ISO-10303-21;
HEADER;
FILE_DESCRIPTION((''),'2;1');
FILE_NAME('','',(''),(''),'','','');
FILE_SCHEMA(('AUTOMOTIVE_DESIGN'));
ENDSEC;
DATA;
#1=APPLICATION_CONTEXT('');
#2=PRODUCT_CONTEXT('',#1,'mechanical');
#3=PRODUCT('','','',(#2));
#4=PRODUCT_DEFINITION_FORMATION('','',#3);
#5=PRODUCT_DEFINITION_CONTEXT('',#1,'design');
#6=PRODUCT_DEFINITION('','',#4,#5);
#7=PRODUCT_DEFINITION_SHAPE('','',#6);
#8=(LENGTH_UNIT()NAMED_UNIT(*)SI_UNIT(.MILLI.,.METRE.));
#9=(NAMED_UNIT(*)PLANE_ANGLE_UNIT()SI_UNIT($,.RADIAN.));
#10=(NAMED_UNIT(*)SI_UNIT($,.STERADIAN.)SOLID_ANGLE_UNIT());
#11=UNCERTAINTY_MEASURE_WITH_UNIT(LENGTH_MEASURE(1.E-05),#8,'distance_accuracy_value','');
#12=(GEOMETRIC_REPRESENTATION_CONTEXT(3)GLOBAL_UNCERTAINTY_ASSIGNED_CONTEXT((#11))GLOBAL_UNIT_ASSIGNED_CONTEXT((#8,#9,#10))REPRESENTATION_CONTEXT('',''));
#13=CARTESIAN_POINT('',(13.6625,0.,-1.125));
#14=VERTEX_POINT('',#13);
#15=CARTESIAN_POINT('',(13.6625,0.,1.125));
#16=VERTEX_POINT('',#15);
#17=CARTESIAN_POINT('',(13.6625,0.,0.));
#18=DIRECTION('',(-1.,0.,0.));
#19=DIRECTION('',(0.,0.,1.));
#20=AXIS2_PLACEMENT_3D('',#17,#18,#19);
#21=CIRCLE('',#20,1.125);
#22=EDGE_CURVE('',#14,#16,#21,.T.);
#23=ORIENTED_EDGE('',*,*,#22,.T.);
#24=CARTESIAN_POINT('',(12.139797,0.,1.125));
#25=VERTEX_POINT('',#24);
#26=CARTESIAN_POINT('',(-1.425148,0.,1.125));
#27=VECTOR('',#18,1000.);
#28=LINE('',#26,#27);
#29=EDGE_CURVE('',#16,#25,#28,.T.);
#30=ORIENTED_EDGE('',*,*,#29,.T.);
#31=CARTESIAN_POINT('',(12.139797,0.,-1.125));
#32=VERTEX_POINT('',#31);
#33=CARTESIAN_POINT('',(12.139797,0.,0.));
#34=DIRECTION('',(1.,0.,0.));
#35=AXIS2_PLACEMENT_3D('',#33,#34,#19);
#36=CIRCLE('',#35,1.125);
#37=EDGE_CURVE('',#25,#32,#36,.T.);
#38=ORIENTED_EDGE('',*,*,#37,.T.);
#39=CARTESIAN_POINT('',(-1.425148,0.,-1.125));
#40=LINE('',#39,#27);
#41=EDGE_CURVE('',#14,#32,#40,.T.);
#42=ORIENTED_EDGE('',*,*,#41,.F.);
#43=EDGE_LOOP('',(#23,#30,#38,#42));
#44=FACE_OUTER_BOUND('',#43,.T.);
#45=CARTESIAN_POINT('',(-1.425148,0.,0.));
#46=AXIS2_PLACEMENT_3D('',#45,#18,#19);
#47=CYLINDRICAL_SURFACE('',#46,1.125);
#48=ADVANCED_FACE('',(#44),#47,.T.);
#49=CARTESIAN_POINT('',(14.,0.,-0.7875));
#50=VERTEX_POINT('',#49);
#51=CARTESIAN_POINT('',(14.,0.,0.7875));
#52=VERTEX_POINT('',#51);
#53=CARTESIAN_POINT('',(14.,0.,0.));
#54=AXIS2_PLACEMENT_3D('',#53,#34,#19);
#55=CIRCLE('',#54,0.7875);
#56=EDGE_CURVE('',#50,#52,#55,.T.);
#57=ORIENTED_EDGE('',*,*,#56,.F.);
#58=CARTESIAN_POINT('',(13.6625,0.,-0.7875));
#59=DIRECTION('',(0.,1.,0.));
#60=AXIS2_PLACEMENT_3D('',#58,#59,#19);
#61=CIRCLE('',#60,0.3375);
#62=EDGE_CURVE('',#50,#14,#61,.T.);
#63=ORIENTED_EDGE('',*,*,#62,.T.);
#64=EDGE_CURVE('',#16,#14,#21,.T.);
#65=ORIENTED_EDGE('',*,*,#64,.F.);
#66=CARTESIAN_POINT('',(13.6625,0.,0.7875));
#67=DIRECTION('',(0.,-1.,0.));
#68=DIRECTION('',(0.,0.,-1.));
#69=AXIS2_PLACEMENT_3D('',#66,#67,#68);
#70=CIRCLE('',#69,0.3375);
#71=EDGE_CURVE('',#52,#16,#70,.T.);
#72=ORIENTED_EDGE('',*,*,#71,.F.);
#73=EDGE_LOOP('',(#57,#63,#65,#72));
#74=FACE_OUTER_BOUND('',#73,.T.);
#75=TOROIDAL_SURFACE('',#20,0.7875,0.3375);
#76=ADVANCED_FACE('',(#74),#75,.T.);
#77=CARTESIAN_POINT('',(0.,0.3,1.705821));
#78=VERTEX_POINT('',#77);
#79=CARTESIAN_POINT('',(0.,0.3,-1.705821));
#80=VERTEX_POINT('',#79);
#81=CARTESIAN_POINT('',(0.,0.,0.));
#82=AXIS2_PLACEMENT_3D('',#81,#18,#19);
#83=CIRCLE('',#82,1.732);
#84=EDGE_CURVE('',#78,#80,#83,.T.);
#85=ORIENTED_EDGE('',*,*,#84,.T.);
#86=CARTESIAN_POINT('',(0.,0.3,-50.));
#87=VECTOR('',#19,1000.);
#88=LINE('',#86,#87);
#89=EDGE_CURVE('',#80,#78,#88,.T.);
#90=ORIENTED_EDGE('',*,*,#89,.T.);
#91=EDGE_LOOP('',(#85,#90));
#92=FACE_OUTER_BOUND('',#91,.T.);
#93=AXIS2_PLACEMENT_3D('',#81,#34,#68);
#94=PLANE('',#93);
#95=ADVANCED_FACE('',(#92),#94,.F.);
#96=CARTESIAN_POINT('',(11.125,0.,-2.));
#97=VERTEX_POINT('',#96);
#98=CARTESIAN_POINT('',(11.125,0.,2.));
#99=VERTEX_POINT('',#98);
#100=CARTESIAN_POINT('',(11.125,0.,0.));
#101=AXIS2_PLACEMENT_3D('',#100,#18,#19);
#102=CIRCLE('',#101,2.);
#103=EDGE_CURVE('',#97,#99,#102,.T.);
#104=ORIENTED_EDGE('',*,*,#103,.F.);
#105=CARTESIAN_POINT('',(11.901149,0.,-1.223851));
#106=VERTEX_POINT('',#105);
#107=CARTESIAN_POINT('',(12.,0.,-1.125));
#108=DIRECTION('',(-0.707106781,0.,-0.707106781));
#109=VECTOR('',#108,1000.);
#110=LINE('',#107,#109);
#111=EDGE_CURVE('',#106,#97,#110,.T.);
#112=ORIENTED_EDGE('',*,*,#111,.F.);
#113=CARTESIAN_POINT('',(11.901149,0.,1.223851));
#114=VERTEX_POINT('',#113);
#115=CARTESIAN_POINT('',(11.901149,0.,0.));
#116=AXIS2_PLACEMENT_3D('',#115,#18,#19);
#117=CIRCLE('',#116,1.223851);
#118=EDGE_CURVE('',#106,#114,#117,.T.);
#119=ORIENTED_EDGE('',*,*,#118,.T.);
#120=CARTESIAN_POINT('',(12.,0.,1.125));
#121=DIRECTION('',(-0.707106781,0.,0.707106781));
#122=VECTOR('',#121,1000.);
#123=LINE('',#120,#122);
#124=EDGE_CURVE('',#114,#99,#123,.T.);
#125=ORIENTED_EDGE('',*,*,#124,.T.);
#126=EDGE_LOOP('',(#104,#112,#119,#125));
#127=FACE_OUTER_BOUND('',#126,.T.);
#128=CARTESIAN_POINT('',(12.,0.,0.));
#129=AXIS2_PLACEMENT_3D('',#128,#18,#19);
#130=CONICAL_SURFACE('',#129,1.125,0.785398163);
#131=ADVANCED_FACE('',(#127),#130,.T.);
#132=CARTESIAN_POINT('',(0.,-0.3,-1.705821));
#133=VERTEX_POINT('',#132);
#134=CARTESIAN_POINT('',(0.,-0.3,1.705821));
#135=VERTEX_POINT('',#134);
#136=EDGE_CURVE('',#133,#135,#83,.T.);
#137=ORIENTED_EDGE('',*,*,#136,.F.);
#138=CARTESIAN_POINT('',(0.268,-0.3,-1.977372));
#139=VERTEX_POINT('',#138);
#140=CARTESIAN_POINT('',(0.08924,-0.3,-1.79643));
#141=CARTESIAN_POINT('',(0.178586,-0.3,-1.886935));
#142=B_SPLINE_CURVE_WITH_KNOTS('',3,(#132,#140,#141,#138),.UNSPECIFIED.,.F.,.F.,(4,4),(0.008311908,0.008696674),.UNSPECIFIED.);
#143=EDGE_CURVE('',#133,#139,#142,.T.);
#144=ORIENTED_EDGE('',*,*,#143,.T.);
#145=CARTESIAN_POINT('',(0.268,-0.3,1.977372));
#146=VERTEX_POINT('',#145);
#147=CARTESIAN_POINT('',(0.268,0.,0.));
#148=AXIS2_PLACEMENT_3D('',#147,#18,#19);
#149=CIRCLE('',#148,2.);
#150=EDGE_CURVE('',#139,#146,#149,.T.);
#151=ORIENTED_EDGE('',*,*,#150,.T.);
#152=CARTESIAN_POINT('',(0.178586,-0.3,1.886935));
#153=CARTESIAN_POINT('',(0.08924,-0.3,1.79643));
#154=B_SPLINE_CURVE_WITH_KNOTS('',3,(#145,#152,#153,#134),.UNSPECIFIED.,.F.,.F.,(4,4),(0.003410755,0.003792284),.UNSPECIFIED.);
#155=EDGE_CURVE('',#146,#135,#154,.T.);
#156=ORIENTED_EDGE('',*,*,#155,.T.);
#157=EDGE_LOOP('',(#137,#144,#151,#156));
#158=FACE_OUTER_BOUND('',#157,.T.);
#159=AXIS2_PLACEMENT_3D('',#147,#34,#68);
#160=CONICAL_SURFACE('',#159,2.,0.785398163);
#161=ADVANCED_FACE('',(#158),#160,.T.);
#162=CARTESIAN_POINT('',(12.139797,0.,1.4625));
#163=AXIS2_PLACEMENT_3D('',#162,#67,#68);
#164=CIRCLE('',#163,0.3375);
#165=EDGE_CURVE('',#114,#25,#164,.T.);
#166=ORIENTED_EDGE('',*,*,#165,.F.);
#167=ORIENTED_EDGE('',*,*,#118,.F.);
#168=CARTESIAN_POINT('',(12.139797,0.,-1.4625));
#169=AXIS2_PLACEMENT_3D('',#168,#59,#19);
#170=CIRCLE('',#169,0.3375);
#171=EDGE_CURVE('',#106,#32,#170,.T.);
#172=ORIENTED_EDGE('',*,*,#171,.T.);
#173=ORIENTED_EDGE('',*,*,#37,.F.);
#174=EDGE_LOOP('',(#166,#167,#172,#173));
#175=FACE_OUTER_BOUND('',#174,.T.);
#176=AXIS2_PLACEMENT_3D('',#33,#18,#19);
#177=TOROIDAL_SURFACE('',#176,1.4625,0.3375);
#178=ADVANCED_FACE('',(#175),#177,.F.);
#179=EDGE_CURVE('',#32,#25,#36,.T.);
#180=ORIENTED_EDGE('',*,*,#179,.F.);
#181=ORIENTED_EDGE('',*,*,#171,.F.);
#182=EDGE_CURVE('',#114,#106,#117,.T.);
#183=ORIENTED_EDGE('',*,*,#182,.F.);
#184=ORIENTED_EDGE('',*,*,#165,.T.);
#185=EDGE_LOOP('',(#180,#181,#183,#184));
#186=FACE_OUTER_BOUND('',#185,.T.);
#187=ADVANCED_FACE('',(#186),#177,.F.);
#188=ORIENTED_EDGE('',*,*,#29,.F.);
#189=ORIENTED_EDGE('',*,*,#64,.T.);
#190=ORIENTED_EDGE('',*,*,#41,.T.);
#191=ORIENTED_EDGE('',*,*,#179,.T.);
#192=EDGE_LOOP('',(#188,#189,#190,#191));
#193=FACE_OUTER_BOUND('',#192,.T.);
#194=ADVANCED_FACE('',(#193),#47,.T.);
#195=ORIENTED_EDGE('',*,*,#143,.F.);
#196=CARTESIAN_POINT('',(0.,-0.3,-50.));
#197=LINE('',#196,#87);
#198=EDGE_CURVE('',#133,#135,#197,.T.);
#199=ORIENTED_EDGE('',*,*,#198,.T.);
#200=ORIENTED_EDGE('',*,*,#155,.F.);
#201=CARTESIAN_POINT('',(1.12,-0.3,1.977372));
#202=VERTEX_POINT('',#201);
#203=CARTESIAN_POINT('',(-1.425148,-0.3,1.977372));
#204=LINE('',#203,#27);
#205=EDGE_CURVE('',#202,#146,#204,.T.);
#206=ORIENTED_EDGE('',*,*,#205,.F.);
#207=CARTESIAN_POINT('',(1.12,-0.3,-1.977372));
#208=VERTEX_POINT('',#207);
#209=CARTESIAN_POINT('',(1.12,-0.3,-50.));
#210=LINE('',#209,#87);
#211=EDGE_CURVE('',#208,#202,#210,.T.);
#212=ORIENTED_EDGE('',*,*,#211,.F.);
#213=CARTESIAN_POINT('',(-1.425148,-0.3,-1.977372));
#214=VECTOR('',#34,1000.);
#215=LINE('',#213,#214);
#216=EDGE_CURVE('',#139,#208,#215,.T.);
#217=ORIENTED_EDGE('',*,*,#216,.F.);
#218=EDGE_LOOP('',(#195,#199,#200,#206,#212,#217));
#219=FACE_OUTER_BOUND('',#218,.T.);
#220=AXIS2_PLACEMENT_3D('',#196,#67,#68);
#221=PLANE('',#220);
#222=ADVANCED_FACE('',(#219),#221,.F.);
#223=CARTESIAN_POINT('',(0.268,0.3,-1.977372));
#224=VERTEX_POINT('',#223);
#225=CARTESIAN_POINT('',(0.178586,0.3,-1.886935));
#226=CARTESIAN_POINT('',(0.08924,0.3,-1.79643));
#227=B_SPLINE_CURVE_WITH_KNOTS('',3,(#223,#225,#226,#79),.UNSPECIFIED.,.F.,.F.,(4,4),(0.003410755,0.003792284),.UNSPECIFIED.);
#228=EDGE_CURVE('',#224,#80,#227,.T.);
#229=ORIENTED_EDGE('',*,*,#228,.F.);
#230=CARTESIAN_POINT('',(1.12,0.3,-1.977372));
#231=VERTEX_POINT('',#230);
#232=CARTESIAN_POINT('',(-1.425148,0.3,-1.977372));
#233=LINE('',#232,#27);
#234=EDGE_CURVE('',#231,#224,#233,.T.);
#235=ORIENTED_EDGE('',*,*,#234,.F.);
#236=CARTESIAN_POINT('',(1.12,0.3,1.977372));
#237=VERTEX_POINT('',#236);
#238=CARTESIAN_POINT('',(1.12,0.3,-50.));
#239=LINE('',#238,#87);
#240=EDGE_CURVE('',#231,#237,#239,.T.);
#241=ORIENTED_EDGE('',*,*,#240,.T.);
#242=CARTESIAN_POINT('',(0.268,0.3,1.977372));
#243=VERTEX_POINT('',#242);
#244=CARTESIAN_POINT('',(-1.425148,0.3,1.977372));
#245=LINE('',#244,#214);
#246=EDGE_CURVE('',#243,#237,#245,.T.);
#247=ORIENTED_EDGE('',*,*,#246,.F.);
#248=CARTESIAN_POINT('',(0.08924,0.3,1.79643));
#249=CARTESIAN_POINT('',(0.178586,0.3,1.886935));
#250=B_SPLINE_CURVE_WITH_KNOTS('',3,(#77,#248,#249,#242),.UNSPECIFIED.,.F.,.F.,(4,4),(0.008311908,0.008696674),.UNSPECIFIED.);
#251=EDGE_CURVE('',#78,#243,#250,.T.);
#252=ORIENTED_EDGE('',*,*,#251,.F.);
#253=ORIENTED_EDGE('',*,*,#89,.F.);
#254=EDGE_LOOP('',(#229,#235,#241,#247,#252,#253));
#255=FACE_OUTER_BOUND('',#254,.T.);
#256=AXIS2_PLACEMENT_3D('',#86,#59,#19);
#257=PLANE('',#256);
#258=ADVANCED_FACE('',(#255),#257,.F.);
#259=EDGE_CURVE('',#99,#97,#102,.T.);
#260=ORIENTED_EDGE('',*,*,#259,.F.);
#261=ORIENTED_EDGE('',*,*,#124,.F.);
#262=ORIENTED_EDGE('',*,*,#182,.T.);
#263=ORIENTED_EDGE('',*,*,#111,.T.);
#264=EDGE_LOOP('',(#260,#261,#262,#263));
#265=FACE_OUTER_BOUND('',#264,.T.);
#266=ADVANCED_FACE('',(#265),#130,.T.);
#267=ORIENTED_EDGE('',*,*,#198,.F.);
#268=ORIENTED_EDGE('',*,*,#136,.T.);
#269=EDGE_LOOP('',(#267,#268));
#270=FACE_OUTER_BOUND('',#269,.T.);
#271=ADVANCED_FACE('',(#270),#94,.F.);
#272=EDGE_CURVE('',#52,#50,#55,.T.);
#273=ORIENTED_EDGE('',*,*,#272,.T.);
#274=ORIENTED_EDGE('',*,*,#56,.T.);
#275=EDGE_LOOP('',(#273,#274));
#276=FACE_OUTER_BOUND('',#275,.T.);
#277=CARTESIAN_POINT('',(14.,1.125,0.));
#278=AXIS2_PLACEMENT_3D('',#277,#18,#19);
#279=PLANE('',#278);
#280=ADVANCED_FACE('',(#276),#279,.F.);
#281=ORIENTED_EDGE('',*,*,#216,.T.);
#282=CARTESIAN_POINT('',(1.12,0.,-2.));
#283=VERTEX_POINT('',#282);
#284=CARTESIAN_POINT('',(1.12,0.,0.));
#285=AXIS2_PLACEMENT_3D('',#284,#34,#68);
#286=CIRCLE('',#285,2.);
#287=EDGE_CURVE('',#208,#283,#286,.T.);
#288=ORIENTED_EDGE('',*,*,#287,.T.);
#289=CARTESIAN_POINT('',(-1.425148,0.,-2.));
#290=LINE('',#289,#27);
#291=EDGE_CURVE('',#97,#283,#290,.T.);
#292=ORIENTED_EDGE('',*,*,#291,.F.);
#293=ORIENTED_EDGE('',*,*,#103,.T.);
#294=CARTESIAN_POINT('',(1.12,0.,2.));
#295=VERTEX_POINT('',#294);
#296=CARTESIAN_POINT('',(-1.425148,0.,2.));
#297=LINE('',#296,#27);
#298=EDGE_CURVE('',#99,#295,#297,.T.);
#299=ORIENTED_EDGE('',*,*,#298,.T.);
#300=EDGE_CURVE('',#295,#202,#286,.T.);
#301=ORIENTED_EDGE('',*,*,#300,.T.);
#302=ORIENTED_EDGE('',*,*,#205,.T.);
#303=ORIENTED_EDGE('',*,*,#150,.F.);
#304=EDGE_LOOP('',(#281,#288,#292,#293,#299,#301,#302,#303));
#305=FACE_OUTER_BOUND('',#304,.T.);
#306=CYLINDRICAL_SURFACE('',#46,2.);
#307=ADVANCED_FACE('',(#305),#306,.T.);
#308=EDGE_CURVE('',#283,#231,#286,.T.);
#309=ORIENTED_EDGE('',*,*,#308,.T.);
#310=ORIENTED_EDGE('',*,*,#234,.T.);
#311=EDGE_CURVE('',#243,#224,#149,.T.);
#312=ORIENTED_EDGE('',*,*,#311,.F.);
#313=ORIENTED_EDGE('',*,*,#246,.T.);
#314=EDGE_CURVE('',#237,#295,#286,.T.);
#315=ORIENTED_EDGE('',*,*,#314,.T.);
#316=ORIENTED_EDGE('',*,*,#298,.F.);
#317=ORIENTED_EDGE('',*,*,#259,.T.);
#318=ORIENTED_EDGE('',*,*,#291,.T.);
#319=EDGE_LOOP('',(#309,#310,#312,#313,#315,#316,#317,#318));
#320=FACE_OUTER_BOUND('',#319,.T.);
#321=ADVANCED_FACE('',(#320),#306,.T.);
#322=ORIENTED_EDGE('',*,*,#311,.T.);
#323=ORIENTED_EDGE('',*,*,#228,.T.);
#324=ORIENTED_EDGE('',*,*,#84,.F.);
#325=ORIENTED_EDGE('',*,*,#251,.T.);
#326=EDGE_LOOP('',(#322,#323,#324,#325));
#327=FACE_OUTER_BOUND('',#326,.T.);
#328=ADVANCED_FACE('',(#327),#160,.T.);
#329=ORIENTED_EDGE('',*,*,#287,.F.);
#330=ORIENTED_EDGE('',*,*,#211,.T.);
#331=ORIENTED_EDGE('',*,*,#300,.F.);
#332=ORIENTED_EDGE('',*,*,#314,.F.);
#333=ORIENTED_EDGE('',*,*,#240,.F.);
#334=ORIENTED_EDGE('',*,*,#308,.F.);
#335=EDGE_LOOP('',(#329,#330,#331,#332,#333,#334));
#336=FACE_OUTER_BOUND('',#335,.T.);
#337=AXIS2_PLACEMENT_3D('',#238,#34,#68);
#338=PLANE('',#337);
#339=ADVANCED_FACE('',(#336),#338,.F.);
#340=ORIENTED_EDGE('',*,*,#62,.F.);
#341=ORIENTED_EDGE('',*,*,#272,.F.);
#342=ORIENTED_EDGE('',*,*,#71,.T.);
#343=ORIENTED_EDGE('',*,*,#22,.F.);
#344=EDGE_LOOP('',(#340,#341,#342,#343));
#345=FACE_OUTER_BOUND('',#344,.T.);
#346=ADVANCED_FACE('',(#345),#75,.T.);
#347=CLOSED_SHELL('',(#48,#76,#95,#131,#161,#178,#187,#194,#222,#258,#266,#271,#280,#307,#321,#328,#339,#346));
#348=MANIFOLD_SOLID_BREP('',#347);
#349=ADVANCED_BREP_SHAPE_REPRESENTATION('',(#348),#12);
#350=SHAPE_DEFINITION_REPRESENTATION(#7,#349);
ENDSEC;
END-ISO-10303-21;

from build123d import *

# Parameters (mm, degrees)
SKETCH4_W          = 1.12
SKETCH4_H          = 0.6
CUT_EXTRUDE1_DEPTH = 50
FILLET1_R          = 0.3375


with BuildPart() as part:
    # Sketch3 → Base-Revolve (revolve)
    with BuildSketch(Plane.XY, mode=Mode.PRIVATE) as base_revolve_sk:
        Polygon((0, 0), (0, 1.732), (0.268, 2), (11.125, 2), (12, 1.125), (14, 1.125), (14, 0), align=None)
    revolve(base_revolve_sk.sketch.rotate(Axis((0, 0, 0), (1, 0, 0)), 90), axis=Axis((0, 0, 0), (1, 0, 0)))

    # Sketch4 → Cut-Extrude1 (cut, symmetric)
    with BuildSketch(Plane.XY):
        with Locations((0.56, 0)):
            Rectangle(SKETCH4_W, SKETCH4_H)
    extrude(amount=CUT_EXTRUDE1_DEPTH, both=True, mode=Mode.SUBTRACT)

    # Fillet1
    fillet1_edges = [part.edges().sort_by_distance(p)[0] for p in [
        (14, 0, -1.125),
        (12, 0, -1.125),
    ]]
    fillet(fillet1_edges, radius=FILLET1_R)


solid = part.part
